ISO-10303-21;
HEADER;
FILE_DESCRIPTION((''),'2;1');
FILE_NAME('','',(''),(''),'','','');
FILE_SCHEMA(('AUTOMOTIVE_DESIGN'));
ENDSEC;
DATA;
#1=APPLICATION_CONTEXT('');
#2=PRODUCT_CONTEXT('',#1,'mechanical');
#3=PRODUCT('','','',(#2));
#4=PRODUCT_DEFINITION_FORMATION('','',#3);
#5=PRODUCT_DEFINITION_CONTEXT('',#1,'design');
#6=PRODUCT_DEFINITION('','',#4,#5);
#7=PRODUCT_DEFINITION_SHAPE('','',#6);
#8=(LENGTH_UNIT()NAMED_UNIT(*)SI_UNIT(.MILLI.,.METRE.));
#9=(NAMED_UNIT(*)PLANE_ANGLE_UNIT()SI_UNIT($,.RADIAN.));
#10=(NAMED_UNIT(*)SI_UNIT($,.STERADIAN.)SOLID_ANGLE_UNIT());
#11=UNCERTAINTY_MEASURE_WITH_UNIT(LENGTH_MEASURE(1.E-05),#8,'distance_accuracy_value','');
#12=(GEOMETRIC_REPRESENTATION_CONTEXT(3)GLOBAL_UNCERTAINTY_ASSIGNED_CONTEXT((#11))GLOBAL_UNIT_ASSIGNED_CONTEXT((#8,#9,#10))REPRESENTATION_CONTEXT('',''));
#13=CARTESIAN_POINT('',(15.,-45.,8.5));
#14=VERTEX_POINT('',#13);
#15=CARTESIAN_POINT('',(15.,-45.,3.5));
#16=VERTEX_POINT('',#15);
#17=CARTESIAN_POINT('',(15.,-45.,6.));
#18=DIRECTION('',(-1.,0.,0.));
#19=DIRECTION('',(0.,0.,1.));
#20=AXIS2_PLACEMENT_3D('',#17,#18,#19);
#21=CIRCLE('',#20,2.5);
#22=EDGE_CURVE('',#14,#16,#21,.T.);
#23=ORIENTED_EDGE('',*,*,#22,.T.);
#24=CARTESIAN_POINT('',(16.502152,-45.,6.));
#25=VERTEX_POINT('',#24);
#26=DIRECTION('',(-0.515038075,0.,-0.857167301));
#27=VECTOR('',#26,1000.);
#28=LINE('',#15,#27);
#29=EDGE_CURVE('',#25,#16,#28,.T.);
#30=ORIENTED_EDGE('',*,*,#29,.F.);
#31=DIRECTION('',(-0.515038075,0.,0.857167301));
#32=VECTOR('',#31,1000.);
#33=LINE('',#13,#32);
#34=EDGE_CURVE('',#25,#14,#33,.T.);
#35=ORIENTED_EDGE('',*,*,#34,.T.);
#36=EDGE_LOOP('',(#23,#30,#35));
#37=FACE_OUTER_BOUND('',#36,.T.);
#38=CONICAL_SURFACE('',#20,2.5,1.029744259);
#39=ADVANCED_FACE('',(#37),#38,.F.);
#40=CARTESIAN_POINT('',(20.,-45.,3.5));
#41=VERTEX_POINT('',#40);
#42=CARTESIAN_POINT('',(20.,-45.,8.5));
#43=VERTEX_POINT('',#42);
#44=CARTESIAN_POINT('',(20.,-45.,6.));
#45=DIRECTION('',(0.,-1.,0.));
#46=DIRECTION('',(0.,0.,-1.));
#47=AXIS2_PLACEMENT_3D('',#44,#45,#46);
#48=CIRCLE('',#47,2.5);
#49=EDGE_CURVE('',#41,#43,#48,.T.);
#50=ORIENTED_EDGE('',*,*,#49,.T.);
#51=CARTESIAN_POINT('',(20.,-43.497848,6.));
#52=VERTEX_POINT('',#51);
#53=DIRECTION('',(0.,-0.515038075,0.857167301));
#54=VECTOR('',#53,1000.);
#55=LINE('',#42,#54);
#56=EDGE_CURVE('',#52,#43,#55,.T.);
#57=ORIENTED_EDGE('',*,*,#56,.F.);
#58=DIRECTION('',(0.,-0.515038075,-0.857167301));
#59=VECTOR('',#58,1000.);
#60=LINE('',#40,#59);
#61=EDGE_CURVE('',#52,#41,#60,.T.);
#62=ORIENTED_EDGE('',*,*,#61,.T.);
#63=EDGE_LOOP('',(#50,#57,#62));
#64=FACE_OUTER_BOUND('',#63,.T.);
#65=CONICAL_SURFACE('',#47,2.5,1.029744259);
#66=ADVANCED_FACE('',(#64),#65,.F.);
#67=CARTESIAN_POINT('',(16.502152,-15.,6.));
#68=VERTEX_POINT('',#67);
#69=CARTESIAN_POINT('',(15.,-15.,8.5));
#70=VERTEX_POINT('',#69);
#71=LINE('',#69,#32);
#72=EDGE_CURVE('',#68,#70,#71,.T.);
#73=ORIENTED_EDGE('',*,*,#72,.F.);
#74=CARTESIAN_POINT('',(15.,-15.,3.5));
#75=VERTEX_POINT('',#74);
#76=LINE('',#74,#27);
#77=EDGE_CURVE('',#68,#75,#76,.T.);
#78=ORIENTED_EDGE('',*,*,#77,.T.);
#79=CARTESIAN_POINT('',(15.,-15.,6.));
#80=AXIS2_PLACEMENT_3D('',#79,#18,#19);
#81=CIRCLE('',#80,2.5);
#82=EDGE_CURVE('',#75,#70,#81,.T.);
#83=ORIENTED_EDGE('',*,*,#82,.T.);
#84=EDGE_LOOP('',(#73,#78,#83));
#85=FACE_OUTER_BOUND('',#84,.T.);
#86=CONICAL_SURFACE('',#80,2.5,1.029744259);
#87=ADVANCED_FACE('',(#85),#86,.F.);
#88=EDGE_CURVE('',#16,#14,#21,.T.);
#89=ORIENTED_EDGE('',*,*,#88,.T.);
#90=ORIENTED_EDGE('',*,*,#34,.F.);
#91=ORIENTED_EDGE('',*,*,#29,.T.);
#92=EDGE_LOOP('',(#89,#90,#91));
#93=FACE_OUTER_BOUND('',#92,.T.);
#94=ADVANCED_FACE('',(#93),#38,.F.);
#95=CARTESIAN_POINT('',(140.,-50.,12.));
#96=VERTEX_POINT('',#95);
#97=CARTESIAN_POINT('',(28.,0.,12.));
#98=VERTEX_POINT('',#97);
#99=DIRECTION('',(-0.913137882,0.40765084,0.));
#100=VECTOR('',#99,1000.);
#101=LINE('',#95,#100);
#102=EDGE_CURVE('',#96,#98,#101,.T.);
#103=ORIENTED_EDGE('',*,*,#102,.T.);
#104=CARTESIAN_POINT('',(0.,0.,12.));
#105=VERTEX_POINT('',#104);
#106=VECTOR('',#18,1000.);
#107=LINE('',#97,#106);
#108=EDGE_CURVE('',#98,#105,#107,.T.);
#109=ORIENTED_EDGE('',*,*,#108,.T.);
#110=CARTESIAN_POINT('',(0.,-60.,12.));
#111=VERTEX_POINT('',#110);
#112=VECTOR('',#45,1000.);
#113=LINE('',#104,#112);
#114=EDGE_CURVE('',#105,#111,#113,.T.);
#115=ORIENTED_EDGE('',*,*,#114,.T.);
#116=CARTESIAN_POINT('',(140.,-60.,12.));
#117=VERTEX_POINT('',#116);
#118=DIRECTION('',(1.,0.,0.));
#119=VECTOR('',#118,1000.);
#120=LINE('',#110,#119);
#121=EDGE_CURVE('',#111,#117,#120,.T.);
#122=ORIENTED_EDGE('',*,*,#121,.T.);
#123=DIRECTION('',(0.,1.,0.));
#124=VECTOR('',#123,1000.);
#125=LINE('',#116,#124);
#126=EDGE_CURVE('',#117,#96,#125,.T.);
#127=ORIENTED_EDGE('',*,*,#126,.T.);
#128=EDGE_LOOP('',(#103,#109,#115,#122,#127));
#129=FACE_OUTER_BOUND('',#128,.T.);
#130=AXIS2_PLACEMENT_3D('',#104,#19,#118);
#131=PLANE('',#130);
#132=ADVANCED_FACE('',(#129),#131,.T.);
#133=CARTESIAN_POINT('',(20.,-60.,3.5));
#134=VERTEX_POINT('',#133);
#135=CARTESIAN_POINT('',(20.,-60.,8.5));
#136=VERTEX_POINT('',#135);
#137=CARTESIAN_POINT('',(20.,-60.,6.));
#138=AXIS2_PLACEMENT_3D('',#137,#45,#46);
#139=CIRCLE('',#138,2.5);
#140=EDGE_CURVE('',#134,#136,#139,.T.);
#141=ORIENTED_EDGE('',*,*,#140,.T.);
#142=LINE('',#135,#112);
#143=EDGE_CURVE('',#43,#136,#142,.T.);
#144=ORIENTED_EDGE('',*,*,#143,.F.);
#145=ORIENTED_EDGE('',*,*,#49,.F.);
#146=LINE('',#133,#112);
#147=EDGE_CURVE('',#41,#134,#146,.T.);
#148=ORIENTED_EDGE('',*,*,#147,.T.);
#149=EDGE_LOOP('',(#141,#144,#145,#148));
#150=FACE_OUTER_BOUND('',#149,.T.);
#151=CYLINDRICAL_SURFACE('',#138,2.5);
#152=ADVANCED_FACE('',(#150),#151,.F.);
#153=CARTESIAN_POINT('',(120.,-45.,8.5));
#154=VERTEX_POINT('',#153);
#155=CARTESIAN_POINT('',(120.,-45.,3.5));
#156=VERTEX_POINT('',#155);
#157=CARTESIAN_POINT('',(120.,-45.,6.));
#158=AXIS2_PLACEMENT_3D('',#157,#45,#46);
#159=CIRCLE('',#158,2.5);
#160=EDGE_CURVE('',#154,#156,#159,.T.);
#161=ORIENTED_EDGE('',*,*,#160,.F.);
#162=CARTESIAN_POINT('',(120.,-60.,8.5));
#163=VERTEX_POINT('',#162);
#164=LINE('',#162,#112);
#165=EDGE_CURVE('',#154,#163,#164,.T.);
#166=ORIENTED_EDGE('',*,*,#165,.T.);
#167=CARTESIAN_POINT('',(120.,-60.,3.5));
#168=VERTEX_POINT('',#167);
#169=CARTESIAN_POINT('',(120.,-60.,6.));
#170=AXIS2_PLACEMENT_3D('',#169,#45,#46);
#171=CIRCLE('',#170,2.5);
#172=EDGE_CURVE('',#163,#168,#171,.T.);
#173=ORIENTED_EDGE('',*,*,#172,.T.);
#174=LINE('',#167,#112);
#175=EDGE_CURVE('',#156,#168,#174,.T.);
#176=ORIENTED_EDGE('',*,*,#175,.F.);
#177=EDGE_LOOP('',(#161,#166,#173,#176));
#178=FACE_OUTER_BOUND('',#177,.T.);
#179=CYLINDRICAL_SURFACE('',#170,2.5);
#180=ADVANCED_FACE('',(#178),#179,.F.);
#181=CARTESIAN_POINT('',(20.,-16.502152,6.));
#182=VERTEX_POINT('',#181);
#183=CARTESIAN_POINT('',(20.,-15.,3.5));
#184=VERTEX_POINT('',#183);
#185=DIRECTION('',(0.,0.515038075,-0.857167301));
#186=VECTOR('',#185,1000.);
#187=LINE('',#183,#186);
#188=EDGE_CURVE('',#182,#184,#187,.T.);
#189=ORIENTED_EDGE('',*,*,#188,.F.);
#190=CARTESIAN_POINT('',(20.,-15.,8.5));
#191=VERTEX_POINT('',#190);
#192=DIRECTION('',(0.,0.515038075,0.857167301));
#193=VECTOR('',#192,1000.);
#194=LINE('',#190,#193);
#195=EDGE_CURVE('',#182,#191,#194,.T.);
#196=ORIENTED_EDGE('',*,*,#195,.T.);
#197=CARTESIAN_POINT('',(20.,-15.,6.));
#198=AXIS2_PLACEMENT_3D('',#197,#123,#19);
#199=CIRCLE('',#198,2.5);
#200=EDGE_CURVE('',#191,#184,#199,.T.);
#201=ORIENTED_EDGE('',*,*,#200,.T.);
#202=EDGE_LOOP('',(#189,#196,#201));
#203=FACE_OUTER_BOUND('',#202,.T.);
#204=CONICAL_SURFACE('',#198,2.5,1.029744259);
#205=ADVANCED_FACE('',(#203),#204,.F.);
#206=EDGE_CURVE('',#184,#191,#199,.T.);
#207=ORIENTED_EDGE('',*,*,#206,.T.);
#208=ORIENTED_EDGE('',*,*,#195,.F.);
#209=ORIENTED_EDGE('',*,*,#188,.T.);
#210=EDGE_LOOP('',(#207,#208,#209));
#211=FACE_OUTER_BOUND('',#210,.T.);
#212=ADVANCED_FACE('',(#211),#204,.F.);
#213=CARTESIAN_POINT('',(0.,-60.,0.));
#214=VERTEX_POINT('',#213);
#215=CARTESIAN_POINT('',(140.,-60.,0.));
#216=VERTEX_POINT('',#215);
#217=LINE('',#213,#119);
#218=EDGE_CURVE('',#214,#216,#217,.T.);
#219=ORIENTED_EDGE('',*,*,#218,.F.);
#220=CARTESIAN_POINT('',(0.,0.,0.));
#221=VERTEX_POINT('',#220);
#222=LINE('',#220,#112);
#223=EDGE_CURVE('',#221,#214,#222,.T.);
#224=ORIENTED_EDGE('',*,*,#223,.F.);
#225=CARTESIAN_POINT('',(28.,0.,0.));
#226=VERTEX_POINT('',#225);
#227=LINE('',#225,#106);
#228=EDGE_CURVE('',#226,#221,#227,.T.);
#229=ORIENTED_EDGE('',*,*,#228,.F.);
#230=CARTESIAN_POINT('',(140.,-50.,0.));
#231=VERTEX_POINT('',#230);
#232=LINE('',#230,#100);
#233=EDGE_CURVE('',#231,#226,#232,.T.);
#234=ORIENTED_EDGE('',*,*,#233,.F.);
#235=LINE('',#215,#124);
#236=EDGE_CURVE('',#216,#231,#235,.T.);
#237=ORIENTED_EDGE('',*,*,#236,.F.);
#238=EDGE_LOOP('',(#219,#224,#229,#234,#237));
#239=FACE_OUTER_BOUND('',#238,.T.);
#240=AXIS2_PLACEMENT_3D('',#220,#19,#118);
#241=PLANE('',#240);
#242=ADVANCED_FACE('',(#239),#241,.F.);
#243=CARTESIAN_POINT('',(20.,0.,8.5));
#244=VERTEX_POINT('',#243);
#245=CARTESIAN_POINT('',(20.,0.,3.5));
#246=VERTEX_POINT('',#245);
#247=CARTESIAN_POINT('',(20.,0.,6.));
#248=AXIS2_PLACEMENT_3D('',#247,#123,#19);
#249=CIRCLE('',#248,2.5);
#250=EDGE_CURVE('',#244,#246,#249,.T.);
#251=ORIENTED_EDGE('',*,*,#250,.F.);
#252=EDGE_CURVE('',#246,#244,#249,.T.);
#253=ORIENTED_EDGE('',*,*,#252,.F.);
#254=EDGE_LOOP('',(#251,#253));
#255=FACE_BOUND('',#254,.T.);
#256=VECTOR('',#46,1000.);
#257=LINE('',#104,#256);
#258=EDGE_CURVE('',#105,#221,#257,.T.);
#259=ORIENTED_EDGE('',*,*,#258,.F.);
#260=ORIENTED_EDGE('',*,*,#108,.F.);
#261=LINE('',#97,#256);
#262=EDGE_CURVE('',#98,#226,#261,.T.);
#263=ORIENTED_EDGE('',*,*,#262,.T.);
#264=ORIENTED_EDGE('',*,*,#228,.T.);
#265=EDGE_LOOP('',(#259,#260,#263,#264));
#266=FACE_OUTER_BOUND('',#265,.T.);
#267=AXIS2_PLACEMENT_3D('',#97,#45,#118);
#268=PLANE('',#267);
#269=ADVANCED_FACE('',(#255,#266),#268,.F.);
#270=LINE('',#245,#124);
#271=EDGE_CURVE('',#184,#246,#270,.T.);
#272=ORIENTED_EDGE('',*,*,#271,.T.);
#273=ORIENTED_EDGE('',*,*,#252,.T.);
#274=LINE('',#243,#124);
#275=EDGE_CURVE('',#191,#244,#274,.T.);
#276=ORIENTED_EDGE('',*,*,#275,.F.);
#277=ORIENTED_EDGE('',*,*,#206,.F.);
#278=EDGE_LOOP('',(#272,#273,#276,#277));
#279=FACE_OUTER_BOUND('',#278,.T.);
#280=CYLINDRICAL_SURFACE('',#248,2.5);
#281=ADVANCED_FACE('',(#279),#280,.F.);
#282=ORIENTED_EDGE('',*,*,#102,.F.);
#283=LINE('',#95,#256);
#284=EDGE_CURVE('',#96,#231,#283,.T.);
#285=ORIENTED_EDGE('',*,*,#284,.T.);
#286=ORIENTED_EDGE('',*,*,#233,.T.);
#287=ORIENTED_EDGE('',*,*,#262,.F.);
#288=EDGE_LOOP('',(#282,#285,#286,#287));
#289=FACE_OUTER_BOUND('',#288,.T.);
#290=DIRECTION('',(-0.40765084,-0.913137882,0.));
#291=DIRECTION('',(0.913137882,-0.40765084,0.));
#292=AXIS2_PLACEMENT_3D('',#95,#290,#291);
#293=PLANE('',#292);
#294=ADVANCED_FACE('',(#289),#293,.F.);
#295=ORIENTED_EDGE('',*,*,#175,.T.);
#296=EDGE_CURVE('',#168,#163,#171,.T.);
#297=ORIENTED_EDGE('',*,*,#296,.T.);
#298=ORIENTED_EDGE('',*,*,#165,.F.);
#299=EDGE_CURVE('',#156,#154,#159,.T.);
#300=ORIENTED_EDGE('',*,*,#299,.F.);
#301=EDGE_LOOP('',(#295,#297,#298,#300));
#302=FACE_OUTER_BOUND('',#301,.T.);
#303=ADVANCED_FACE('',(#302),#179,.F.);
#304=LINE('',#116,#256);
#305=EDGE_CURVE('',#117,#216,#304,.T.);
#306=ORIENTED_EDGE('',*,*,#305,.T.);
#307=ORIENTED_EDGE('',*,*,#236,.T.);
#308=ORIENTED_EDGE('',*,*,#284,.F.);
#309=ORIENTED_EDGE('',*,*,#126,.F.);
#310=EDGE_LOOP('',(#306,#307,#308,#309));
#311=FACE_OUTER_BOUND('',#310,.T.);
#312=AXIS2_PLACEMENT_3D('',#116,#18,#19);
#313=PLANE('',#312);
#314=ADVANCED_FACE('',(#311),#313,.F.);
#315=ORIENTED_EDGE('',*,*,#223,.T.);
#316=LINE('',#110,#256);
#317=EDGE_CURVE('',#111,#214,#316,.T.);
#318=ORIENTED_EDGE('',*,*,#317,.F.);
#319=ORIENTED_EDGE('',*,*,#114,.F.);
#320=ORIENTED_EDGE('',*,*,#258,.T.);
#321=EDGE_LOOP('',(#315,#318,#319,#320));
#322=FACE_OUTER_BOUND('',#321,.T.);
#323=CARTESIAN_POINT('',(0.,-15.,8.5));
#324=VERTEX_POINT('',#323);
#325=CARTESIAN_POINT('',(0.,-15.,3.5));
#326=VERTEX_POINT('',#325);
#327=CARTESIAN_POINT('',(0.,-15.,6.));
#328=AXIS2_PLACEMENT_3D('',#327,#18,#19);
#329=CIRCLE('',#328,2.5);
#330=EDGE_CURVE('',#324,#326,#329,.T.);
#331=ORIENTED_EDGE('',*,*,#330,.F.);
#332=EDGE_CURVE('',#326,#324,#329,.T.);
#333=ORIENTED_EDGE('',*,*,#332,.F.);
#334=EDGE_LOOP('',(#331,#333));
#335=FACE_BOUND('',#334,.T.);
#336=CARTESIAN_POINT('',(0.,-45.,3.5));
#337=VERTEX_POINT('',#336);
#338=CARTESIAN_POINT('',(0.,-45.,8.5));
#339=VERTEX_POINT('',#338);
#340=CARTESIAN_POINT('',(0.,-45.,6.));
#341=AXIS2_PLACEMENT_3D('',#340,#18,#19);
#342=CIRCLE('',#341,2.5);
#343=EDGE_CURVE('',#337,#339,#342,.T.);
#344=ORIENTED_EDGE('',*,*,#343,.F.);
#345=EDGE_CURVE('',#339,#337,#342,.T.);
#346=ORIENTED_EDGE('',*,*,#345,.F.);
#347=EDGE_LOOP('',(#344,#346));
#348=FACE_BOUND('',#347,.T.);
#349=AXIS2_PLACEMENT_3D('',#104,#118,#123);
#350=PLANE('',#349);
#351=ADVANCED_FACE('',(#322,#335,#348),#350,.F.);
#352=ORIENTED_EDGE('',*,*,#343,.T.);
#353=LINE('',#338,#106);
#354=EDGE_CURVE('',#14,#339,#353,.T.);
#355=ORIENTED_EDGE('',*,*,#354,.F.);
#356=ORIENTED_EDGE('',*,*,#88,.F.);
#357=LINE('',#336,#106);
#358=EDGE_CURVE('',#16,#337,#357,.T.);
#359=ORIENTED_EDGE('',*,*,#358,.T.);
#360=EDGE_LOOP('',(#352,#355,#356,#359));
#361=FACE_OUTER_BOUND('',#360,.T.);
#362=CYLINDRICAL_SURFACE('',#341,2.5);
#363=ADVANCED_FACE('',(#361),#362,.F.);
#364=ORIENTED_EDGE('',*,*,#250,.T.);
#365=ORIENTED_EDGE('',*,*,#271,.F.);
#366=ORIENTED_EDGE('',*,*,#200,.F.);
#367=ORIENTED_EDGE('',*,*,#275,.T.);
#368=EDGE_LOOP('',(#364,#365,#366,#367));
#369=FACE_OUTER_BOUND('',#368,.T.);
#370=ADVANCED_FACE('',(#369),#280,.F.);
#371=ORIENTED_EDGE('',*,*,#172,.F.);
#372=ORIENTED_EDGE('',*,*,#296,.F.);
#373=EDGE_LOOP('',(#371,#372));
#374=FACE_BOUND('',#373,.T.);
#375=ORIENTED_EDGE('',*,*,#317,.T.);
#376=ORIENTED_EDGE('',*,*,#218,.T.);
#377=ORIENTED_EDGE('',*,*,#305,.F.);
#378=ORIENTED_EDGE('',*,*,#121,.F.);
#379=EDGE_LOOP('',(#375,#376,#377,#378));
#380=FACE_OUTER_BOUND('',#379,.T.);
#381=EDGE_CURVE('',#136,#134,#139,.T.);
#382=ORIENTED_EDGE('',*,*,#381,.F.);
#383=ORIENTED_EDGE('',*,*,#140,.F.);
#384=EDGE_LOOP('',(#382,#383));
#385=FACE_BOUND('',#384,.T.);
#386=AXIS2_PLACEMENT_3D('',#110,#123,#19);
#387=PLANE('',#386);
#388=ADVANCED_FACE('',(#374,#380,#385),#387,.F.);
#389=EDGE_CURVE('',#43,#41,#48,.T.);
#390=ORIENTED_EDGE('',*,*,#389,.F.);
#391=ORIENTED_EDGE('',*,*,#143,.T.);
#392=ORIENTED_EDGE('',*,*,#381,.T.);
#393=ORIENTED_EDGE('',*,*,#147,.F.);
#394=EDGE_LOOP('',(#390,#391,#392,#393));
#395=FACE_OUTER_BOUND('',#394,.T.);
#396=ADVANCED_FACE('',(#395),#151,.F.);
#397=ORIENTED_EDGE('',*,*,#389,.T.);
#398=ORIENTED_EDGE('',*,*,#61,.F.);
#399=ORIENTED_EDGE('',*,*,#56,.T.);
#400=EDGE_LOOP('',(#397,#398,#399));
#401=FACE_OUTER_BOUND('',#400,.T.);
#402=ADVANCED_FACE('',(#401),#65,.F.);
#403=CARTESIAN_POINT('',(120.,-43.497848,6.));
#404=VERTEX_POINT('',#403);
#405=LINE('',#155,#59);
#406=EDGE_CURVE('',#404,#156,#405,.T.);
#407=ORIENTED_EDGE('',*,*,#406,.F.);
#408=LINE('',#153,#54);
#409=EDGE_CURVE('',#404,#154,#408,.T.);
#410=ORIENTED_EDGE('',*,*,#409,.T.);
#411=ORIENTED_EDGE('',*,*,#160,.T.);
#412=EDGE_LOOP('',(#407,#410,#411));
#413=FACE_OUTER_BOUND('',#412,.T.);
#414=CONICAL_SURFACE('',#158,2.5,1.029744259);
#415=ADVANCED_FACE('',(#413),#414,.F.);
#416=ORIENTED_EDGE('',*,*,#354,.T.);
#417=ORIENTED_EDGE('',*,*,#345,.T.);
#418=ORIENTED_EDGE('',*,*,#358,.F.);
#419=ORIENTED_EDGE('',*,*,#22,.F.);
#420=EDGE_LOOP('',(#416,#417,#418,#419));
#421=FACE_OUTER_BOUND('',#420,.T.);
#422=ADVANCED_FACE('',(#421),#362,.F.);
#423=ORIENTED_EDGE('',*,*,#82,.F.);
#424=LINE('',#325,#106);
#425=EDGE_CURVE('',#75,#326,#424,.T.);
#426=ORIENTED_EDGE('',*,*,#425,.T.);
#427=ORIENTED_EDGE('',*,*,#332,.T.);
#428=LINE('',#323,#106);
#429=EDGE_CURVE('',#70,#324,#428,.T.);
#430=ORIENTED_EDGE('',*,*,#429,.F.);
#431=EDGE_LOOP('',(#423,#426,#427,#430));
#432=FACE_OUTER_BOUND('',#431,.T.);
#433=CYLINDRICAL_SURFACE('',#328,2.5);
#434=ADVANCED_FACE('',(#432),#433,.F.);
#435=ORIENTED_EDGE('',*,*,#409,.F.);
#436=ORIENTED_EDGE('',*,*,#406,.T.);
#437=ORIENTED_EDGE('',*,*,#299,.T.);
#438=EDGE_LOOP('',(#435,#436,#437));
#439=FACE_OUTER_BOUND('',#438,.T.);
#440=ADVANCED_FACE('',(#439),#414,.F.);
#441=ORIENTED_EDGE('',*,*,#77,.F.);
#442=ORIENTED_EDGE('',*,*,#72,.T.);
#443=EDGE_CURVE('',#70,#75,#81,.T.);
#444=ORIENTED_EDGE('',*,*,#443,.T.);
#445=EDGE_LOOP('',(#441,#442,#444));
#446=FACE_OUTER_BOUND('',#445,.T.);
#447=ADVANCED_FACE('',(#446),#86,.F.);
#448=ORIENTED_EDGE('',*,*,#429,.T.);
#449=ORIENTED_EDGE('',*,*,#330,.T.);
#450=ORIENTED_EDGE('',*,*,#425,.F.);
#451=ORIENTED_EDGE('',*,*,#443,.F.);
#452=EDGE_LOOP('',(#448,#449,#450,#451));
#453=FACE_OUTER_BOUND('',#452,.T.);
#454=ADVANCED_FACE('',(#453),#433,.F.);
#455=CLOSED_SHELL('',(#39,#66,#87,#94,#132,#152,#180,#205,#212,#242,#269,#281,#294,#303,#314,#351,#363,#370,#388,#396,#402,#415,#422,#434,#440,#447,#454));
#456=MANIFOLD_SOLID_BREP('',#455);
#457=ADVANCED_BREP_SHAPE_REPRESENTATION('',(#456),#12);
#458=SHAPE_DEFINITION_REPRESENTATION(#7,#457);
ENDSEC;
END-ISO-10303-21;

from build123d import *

# Parameters (mm, degrees)
EXTRUDE_1_DEPTH        = 12
HOLE_WIZARD_M6_1_D     = 5
HOLE_WIZARD_M6_1_DEPTH = 15
HOLE_WIZARD_M6_1_TIP   = 1.502151548
HOLE_WIZARD_M6_2_D     = 5
HOLE_WIZARD_M6_2_DEPTH = 15
HOLE_WIZARD_M6_2_TIP   = 1.502151548
HOLE_WIZARD_M6_3_D     = 5
HOLE_WIZARD_M6_3_DEPTH = 15
HOLE_WIZARD_M6_3_TIP   = 1.502151548


with BuildPart() as part:
    # 草图1 → 凸台-拉伸1 (new body)
    with BuildSketch(Plane.XY):
        Polygon((0, 0), (0, -60), (140, -60), (140, -50), (28, 0), align=None)
    extrude(amount=EXTRUDE_1_DEPTH)

    # M6 螺纹孔1
    with Locations(Plane.ZY):
        with Locations((6, -15), (6, -45)):
            Hole(HOLE_WIZARD_M6_1_D / 2, depth=HOLE_WIZARD_M6_1_DEPTH)
            with Locations((0, 0, -(HOLE_WIZARD_M6_1_DEPTH + HOLE_WIZARD_M6_1_TIP / 2))):  # 118° drill point
                Cone(0, HOLE_WIZARD_M6_1_D / 2, HOLE_WIZARD_M6_1_TIP, mode=Mode.SUBTRACT)

    # M6 螺纹孔2
    with Locations(Plane(origin=(0, -60, 0), x_dir=(-1, 0, 0), z_dir=(0, -1, 0))):
        with Locations((-120, -6), (-20, -6)):
            Hole(HOLE_WIZARD_M6_2_D / 2, depth=HOLE_WIZARD_M6_2_DEPTH)
            with Locations((0, 0, -(HOLE_WIZARD_M6_2_DEPTH + HOLE_WIZARD_M6_2_TIP / 2))):  # 118° drill point
                Cone(0, HOLE_WIZARD_M6_2_D / 2, HOLE_WIZARD_M6_2_TIP, mode=Mode.SUBTRACT)

    # M6 螺纹孔3
    with Locations(Plane(origin=(0, 0, 0), x_dir=(1, 0, 0), z_dir=(0, 1, 0))):
        with Locations((20, -6)):
            Hole(HOLE_WIZARD_M6_3_D / 2, depth=HOLE_WIZARD_M6_3_DEPTH)
            with Locations((0, 0, -(HOLE_WIZARD_M6_3_DEPTH + HOLE_WIZARD_M6_3_TIP / 2))):  # 118° drill point
                Cone(0, HOLE_WIZARD_M6_3_D / 2, HOLE_WIZARD_M6_3_TIP, mode=Mode.SUBTRACT)


solid = part.part
